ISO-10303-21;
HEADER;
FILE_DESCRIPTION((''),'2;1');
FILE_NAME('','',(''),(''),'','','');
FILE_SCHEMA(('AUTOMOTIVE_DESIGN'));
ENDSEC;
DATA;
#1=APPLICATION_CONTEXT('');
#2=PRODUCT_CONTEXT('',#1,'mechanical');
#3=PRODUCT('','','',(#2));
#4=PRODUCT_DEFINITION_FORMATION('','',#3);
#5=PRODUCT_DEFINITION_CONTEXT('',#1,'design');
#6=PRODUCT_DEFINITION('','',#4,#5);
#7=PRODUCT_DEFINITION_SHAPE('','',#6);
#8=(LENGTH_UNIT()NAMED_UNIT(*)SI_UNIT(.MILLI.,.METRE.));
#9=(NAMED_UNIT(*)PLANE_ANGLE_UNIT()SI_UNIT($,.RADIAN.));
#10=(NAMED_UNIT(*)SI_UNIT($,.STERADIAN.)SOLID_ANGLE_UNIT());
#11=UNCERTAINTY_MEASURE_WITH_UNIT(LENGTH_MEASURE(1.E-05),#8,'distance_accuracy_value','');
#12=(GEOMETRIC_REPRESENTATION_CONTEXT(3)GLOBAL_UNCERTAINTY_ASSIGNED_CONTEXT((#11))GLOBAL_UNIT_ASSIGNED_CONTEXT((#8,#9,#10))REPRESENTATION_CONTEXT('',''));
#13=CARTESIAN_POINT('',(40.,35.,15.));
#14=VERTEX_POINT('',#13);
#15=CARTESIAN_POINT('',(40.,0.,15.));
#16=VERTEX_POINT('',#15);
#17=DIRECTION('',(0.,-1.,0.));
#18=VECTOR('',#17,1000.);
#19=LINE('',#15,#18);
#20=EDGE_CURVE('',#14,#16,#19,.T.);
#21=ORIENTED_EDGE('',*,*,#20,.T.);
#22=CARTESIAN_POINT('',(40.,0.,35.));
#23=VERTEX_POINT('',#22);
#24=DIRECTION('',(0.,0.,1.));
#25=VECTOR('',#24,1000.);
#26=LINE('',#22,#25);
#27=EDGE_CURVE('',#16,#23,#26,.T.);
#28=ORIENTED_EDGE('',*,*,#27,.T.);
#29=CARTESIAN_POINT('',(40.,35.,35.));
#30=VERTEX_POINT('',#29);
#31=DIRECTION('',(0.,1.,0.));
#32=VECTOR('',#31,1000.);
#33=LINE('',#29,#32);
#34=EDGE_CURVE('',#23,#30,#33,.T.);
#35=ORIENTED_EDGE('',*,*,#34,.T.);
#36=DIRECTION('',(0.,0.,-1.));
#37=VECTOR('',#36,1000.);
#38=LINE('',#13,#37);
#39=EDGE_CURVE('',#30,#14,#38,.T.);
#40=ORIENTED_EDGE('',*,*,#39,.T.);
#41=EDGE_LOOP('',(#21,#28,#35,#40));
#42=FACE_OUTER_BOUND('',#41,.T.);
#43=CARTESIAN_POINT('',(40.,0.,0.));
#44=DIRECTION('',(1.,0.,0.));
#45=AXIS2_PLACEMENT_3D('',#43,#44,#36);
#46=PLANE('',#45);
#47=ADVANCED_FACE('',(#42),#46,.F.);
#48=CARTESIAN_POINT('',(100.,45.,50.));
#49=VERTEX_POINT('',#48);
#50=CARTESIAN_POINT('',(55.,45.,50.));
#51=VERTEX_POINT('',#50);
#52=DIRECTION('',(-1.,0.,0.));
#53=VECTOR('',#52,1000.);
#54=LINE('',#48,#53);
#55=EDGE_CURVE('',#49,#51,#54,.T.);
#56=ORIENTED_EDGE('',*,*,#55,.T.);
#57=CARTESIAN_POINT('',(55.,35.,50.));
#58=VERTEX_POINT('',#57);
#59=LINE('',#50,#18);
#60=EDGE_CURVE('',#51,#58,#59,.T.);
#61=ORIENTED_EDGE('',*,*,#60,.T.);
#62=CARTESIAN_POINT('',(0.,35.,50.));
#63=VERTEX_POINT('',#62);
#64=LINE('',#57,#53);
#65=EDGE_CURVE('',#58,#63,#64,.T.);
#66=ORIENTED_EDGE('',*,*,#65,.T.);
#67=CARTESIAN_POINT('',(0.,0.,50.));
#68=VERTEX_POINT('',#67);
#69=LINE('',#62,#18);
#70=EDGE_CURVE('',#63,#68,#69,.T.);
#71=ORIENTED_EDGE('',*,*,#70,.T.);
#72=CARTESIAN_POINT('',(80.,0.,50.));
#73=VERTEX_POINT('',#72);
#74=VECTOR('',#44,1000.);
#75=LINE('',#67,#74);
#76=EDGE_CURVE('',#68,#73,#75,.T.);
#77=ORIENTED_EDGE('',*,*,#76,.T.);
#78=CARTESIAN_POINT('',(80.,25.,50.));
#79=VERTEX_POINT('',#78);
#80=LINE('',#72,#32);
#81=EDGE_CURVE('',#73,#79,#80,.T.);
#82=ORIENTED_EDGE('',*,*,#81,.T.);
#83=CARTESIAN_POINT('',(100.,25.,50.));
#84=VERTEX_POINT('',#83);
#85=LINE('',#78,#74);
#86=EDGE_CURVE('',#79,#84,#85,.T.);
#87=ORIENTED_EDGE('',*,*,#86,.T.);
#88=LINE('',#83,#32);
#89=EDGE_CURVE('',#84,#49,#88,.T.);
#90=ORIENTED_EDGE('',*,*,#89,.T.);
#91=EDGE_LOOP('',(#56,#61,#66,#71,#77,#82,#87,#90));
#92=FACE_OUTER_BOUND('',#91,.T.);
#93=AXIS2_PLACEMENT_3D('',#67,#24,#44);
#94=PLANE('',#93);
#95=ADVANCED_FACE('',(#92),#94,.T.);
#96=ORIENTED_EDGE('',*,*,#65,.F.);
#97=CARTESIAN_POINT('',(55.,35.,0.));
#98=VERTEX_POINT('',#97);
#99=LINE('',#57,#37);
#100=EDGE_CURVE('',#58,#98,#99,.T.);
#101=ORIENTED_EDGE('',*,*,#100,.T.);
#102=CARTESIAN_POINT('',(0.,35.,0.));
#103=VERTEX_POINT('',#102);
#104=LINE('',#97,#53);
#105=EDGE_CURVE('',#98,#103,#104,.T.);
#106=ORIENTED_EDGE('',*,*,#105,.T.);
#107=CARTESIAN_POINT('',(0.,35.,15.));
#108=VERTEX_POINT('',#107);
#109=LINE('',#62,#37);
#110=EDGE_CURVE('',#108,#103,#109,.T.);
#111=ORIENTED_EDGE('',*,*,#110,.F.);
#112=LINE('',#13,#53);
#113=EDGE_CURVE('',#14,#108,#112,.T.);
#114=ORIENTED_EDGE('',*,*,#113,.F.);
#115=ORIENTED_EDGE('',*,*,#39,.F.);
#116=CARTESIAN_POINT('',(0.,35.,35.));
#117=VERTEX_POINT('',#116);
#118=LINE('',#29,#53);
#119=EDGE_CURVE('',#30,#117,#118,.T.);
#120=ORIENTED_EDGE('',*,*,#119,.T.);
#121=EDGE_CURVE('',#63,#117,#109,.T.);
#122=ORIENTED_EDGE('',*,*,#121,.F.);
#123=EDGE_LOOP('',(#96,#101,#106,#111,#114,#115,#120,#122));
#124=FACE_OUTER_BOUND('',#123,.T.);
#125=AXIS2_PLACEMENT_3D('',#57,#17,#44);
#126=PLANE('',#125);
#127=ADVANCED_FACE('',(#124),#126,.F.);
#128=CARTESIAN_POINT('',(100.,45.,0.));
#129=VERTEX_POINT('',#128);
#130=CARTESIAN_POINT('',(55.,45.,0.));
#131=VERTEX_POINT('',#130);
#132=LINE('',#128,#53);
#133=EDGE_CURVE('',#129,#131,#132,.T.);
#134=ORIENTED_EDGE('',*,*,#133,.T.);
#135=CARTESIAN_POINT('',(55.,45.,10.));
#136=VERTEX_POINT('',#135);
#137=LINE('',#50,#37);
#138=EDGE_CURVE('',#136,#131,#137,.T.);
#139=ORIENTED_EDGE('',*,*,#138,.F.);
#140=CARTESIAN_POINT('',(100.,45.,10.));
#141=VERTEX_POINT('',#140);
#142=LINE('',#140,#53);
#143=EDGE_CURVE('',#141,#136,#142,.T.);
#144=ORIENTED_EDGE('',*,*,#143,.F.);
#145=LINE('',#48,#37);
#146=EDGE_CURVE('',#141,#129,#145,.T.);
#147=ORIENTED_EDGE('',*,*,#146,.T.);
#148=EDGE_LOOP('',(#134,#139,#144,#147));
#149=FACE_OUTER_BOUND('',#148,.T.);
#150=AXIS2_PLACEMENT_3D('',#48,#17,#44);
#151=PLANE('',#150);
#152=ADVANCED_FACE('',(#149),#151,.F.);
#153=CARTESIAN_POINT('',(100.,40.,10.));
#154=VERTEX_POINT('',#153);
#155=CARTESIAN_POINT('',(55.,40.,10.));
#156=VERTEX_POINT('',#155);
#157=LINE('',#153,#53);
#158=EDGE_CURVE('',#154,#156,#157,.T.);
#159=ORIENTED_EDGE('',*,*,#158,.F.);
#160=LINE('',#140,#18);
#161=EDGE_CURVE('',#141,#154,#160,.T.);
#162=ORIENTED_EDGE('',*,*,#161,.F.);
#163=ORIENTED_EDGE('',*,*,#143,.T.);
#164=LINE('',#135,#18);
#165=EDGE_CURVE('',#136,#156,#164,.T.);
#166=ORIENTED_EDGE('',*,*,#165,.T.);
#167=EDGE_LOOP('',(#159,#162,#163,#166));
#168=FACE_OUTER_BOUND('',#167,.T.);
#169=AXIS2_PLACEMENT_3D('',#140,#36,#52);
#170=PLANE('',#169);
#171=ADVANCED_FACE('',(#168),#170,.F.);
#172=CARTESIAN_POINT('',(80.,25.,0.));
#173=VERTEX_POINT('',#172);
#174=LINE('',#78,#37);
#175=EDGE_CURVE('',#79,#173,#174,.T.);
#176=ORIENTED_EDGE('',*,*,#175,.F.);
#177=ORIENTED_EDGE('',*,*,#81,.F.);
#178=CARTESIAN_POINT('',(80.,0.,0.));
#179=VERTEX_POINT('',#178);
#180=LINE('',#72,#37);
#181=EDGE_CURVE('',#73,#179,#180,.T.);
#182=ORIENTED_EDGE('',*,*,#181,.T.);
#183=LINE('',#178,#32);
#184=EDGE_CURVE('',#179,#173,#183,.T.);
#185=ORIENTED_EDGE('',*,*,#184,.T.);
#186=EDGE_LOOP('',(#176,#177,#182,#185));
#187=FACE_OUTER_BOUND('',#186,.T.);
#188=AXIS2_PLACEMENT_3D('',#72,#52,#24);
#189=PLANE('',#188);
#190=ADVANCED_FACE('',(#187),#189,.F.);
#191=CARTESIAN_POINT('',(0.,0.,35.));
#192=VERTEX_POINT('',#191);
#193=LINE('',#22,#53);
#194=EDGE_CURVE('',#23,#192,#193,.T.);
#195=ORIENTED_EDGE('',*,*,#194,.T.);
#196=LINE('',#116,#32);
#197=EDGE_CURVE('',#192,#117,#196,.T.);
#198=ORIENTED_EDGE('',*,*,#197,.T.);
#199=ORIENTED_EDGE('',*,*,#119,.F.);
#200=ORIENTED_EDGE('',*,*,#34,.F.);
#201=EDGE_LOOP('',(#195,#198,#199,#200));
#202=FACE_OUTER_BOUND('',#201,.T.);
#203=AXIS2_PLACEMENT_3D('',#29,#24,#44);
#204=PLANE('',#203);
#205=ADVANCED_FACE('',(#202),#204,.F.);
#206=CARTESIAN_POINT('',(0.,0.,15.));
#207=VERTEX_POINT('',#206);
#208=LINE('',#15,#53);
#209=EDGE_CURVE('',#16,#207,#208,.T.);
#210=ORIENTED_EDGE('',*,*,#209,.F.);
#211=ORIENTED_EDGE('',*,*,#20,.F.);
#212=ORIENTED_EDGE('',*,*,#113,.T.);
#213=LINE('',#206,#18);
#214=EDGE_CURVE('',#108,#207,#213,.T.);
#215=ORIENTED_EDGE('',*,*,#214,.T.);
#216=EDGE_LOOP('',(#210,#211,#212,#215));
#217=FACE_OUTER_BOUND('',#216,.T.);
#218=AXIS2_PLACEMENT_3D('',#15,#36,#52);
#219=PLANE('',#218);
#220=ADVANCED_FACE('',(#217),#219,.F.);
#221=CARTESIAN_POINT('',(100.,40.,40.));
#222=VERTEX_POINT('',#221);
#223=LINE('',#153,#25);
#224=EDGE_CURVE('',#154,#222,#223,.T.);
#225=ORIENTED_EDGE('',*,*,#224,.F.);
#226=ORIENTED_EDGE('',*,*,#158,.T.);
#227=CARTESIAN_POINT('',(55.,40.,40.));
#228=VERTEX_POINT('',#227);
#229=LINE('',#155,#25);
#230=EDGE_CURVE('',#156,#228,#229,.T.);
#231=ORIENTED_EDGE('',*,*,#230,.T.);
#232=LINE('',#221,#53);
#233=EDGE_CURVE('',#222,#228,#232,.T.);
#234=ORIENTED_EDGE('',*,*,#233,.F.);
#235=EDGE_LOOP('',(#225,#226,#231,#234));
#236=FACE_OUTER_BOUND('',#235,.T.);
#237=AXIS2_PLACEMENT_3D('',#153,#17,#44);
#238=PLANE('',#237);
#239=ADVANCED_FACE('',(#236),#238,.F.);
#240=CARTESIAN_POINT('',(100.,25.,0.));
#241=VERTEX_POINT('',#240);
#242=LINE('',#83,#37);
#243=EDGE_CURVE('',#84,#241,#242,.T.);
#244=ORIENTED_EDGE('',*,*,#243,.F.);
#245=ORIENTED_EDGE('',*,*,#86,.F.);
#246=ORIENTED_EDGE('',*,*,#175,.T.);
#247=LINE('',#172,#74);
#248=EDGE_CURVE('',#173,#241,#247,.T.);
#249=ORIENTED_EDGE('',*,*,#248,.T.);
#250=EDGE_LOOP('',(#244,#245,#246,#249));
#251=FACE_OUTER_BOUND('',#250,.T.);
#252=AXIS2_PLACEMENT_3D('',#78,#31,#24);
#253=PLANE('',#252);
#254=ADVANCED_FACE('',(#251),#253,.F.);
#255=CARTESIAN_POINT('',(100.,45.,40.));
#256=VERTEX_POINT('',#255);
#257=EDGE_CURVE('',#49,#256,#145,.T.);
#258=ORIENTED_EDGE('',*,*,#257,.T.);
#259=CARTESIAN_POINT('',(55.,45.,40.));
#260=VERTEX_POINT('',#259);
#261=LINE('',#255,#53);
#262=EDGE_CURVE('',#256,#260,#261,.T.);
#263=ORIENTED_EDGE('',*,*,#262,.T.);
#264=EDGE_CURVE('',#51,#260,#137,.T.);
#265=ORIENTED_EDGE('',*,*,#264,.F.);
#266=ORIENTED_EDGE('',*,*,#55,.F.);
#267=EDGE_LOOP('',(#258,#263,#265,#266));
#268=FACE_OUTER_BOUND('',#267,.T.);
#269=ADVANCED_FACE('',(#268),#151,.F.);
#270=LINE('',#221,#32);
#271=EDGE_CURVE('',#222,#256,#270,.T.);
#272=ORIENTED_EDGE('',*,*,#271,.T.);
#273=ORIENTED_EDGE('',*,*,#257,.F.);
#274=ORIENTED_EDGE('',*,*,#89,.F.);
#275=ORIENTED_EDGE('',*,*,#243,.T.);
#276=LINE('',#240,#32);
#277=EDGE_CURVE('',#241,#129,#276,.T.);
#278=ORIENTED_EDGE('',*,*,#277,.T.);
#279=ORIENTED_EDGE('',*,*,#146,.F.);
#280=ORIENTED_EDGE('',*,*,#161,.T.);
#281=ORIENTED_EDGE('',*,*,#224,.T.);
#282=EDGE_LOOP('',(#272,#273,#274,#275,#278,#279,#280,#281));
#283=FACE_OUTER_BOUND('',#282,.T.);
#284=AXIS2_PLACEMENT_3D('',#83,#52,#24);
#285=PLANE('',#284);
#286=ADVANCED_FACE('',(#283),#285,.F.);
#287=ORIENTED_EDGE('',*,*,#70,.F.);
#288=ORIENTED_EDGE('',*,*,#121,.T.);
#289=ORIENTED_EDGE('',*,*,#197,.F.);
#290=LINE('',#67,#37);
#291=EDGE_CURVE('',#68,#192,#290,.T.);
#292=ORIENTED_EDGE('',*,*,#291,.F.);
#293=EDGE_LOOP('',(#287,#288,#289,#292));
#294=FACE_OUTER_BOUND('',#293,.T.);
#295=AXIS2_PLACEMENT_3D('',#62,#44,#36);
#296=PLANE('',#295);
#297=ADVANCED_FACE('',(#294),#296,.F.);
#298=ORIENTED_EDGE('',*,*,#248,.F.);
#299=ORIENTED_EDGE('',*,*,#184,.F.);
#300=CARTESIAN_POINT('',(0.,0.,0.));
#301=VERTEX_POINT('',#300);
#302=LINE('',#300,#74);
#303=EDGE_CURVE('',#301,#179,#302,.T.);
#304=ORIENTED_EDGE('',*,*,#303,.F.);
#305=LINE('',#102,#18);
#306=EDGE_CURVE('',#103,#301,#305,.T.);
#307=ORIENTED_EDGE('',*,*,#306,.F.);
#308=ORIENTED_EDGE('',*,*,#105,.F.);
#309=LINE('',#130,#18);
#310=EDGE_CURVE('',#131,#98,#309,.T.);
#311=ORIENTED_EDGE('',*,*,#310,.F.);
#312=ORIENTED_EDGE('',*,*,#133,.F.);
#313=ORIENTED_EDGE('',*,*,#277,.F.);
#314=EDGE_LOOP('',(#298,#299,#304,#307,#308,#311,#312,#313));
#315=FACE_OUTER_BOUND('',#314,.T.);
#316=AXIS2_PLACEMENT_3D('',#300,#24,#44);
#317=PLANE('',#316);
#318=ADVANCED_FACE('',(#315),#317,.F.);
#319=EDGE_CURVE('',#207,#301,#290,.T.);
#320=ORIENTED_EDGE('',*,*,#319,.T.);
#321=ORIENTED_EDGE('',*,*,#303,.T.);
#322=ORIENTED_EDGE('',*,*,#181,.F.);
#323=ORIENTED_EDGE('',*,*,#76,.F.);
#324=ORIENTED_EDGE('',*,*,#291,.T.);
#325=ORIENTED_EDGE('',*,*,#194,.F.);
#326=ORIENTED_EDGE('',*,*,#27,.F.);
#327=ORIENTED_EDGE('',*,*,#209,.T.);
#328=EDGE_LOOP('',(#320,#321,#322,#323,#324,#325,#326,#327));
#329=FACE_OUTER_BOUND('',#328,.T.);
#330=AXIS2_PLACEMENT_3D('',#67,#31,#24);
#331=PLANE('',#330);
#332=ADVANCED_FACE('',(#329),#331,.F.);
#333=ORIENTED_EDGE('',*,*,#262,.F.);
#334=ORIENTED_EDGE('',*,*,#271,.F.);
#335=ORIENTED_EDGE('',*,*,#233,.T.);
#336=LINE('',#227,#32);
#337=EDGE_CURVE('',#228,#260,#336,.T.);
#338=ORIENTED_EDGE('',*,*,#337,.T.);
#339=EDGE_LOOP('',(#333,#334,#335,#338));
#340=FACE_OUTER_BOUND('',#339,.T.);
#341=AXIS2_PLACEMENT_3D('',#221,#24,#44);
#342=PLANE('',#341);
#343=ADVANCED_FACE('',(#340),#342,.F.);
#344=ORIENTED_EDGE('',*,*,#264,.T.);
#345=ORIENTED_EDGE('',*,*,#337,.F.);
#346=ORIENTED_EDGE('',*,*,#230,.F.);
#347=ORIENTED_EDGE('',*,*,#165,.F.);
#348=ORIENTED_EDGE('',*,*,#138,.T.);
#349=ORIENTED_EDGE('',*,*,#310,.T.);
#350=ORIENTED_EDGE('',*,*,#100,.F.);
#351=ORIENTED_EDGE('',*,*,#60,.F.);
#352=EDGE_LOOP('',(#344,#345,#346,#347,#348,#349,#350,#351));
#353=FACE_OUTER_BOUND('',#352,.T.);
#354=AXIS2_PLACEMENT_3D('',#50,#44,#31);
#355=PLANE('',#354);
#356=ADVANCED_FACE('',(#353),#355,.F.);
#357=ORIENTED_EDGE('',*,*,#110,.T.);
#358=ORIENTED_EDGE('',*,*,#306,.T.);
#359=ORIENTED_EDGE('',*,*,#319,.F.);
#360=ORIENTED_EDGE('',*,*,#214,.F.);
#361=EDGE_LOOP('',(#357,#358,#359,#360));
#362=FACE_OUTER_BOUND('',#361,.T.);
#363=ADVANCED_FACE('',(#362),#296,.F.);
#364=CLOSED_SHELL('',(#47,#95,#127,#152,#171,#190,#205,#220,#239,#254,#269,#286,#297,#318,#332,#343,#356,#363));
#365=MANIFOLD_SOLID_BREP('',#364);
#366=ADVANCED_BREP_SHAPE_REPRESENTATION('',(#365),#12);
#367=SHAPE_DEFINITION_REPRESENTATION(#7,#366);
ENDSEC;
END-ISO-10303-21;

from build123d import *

# Parameters (mm, degrees)
BASE_BLOCK_DEPTH         = 50
POCKET_PROFILE_W         = 20
POCKET_PROFILE_H         = 35
RECTANGULAR_POCKET_DEPTH = 40
SLOT_PROFILE_W           = 30
SLOT_PROFILE_H           = 5
RECTANGULAR_SLOT_DEPTH   = 87.890735985


with BuildPart() as part:
    # Base Block Profile → Base Block (new body)
    with BuildSketch(Plane.XY):
        Polygon((0, 0), (80, 0), (80, 25), (100, 25), (100, 45), (55, 45), (55, 35), (0, 35), align=None)
    extrude(amount=BASE_BLOCK_DEPTH)

    # Pocket Profile → Rectangular Pocket (cut)
    with BuildSketch(Plane.ZY):
        with Locations((25, 17.5)):
            Rectangle(POCKET_PROFILE_W, POCKET_PROFILE_H)
    extrude(amount=-RECTANGULAR_POCKET_DEPTH, mode=Mode.SUBTRACT)

    # Slot Profile → Rectangular Slot (cut, through all)
    with BuildSketch(Plane.ZY.offset(-55)):
        with Locations((25, 42.5)):
            Rectangle(SLOT_PROFILE_W, SLOT_PROFILE_H)
    extrude(amount=-RECTANGULAR_SLOT_DEPTH, mode=Mode.SUBTRACT)


solid = part.part
